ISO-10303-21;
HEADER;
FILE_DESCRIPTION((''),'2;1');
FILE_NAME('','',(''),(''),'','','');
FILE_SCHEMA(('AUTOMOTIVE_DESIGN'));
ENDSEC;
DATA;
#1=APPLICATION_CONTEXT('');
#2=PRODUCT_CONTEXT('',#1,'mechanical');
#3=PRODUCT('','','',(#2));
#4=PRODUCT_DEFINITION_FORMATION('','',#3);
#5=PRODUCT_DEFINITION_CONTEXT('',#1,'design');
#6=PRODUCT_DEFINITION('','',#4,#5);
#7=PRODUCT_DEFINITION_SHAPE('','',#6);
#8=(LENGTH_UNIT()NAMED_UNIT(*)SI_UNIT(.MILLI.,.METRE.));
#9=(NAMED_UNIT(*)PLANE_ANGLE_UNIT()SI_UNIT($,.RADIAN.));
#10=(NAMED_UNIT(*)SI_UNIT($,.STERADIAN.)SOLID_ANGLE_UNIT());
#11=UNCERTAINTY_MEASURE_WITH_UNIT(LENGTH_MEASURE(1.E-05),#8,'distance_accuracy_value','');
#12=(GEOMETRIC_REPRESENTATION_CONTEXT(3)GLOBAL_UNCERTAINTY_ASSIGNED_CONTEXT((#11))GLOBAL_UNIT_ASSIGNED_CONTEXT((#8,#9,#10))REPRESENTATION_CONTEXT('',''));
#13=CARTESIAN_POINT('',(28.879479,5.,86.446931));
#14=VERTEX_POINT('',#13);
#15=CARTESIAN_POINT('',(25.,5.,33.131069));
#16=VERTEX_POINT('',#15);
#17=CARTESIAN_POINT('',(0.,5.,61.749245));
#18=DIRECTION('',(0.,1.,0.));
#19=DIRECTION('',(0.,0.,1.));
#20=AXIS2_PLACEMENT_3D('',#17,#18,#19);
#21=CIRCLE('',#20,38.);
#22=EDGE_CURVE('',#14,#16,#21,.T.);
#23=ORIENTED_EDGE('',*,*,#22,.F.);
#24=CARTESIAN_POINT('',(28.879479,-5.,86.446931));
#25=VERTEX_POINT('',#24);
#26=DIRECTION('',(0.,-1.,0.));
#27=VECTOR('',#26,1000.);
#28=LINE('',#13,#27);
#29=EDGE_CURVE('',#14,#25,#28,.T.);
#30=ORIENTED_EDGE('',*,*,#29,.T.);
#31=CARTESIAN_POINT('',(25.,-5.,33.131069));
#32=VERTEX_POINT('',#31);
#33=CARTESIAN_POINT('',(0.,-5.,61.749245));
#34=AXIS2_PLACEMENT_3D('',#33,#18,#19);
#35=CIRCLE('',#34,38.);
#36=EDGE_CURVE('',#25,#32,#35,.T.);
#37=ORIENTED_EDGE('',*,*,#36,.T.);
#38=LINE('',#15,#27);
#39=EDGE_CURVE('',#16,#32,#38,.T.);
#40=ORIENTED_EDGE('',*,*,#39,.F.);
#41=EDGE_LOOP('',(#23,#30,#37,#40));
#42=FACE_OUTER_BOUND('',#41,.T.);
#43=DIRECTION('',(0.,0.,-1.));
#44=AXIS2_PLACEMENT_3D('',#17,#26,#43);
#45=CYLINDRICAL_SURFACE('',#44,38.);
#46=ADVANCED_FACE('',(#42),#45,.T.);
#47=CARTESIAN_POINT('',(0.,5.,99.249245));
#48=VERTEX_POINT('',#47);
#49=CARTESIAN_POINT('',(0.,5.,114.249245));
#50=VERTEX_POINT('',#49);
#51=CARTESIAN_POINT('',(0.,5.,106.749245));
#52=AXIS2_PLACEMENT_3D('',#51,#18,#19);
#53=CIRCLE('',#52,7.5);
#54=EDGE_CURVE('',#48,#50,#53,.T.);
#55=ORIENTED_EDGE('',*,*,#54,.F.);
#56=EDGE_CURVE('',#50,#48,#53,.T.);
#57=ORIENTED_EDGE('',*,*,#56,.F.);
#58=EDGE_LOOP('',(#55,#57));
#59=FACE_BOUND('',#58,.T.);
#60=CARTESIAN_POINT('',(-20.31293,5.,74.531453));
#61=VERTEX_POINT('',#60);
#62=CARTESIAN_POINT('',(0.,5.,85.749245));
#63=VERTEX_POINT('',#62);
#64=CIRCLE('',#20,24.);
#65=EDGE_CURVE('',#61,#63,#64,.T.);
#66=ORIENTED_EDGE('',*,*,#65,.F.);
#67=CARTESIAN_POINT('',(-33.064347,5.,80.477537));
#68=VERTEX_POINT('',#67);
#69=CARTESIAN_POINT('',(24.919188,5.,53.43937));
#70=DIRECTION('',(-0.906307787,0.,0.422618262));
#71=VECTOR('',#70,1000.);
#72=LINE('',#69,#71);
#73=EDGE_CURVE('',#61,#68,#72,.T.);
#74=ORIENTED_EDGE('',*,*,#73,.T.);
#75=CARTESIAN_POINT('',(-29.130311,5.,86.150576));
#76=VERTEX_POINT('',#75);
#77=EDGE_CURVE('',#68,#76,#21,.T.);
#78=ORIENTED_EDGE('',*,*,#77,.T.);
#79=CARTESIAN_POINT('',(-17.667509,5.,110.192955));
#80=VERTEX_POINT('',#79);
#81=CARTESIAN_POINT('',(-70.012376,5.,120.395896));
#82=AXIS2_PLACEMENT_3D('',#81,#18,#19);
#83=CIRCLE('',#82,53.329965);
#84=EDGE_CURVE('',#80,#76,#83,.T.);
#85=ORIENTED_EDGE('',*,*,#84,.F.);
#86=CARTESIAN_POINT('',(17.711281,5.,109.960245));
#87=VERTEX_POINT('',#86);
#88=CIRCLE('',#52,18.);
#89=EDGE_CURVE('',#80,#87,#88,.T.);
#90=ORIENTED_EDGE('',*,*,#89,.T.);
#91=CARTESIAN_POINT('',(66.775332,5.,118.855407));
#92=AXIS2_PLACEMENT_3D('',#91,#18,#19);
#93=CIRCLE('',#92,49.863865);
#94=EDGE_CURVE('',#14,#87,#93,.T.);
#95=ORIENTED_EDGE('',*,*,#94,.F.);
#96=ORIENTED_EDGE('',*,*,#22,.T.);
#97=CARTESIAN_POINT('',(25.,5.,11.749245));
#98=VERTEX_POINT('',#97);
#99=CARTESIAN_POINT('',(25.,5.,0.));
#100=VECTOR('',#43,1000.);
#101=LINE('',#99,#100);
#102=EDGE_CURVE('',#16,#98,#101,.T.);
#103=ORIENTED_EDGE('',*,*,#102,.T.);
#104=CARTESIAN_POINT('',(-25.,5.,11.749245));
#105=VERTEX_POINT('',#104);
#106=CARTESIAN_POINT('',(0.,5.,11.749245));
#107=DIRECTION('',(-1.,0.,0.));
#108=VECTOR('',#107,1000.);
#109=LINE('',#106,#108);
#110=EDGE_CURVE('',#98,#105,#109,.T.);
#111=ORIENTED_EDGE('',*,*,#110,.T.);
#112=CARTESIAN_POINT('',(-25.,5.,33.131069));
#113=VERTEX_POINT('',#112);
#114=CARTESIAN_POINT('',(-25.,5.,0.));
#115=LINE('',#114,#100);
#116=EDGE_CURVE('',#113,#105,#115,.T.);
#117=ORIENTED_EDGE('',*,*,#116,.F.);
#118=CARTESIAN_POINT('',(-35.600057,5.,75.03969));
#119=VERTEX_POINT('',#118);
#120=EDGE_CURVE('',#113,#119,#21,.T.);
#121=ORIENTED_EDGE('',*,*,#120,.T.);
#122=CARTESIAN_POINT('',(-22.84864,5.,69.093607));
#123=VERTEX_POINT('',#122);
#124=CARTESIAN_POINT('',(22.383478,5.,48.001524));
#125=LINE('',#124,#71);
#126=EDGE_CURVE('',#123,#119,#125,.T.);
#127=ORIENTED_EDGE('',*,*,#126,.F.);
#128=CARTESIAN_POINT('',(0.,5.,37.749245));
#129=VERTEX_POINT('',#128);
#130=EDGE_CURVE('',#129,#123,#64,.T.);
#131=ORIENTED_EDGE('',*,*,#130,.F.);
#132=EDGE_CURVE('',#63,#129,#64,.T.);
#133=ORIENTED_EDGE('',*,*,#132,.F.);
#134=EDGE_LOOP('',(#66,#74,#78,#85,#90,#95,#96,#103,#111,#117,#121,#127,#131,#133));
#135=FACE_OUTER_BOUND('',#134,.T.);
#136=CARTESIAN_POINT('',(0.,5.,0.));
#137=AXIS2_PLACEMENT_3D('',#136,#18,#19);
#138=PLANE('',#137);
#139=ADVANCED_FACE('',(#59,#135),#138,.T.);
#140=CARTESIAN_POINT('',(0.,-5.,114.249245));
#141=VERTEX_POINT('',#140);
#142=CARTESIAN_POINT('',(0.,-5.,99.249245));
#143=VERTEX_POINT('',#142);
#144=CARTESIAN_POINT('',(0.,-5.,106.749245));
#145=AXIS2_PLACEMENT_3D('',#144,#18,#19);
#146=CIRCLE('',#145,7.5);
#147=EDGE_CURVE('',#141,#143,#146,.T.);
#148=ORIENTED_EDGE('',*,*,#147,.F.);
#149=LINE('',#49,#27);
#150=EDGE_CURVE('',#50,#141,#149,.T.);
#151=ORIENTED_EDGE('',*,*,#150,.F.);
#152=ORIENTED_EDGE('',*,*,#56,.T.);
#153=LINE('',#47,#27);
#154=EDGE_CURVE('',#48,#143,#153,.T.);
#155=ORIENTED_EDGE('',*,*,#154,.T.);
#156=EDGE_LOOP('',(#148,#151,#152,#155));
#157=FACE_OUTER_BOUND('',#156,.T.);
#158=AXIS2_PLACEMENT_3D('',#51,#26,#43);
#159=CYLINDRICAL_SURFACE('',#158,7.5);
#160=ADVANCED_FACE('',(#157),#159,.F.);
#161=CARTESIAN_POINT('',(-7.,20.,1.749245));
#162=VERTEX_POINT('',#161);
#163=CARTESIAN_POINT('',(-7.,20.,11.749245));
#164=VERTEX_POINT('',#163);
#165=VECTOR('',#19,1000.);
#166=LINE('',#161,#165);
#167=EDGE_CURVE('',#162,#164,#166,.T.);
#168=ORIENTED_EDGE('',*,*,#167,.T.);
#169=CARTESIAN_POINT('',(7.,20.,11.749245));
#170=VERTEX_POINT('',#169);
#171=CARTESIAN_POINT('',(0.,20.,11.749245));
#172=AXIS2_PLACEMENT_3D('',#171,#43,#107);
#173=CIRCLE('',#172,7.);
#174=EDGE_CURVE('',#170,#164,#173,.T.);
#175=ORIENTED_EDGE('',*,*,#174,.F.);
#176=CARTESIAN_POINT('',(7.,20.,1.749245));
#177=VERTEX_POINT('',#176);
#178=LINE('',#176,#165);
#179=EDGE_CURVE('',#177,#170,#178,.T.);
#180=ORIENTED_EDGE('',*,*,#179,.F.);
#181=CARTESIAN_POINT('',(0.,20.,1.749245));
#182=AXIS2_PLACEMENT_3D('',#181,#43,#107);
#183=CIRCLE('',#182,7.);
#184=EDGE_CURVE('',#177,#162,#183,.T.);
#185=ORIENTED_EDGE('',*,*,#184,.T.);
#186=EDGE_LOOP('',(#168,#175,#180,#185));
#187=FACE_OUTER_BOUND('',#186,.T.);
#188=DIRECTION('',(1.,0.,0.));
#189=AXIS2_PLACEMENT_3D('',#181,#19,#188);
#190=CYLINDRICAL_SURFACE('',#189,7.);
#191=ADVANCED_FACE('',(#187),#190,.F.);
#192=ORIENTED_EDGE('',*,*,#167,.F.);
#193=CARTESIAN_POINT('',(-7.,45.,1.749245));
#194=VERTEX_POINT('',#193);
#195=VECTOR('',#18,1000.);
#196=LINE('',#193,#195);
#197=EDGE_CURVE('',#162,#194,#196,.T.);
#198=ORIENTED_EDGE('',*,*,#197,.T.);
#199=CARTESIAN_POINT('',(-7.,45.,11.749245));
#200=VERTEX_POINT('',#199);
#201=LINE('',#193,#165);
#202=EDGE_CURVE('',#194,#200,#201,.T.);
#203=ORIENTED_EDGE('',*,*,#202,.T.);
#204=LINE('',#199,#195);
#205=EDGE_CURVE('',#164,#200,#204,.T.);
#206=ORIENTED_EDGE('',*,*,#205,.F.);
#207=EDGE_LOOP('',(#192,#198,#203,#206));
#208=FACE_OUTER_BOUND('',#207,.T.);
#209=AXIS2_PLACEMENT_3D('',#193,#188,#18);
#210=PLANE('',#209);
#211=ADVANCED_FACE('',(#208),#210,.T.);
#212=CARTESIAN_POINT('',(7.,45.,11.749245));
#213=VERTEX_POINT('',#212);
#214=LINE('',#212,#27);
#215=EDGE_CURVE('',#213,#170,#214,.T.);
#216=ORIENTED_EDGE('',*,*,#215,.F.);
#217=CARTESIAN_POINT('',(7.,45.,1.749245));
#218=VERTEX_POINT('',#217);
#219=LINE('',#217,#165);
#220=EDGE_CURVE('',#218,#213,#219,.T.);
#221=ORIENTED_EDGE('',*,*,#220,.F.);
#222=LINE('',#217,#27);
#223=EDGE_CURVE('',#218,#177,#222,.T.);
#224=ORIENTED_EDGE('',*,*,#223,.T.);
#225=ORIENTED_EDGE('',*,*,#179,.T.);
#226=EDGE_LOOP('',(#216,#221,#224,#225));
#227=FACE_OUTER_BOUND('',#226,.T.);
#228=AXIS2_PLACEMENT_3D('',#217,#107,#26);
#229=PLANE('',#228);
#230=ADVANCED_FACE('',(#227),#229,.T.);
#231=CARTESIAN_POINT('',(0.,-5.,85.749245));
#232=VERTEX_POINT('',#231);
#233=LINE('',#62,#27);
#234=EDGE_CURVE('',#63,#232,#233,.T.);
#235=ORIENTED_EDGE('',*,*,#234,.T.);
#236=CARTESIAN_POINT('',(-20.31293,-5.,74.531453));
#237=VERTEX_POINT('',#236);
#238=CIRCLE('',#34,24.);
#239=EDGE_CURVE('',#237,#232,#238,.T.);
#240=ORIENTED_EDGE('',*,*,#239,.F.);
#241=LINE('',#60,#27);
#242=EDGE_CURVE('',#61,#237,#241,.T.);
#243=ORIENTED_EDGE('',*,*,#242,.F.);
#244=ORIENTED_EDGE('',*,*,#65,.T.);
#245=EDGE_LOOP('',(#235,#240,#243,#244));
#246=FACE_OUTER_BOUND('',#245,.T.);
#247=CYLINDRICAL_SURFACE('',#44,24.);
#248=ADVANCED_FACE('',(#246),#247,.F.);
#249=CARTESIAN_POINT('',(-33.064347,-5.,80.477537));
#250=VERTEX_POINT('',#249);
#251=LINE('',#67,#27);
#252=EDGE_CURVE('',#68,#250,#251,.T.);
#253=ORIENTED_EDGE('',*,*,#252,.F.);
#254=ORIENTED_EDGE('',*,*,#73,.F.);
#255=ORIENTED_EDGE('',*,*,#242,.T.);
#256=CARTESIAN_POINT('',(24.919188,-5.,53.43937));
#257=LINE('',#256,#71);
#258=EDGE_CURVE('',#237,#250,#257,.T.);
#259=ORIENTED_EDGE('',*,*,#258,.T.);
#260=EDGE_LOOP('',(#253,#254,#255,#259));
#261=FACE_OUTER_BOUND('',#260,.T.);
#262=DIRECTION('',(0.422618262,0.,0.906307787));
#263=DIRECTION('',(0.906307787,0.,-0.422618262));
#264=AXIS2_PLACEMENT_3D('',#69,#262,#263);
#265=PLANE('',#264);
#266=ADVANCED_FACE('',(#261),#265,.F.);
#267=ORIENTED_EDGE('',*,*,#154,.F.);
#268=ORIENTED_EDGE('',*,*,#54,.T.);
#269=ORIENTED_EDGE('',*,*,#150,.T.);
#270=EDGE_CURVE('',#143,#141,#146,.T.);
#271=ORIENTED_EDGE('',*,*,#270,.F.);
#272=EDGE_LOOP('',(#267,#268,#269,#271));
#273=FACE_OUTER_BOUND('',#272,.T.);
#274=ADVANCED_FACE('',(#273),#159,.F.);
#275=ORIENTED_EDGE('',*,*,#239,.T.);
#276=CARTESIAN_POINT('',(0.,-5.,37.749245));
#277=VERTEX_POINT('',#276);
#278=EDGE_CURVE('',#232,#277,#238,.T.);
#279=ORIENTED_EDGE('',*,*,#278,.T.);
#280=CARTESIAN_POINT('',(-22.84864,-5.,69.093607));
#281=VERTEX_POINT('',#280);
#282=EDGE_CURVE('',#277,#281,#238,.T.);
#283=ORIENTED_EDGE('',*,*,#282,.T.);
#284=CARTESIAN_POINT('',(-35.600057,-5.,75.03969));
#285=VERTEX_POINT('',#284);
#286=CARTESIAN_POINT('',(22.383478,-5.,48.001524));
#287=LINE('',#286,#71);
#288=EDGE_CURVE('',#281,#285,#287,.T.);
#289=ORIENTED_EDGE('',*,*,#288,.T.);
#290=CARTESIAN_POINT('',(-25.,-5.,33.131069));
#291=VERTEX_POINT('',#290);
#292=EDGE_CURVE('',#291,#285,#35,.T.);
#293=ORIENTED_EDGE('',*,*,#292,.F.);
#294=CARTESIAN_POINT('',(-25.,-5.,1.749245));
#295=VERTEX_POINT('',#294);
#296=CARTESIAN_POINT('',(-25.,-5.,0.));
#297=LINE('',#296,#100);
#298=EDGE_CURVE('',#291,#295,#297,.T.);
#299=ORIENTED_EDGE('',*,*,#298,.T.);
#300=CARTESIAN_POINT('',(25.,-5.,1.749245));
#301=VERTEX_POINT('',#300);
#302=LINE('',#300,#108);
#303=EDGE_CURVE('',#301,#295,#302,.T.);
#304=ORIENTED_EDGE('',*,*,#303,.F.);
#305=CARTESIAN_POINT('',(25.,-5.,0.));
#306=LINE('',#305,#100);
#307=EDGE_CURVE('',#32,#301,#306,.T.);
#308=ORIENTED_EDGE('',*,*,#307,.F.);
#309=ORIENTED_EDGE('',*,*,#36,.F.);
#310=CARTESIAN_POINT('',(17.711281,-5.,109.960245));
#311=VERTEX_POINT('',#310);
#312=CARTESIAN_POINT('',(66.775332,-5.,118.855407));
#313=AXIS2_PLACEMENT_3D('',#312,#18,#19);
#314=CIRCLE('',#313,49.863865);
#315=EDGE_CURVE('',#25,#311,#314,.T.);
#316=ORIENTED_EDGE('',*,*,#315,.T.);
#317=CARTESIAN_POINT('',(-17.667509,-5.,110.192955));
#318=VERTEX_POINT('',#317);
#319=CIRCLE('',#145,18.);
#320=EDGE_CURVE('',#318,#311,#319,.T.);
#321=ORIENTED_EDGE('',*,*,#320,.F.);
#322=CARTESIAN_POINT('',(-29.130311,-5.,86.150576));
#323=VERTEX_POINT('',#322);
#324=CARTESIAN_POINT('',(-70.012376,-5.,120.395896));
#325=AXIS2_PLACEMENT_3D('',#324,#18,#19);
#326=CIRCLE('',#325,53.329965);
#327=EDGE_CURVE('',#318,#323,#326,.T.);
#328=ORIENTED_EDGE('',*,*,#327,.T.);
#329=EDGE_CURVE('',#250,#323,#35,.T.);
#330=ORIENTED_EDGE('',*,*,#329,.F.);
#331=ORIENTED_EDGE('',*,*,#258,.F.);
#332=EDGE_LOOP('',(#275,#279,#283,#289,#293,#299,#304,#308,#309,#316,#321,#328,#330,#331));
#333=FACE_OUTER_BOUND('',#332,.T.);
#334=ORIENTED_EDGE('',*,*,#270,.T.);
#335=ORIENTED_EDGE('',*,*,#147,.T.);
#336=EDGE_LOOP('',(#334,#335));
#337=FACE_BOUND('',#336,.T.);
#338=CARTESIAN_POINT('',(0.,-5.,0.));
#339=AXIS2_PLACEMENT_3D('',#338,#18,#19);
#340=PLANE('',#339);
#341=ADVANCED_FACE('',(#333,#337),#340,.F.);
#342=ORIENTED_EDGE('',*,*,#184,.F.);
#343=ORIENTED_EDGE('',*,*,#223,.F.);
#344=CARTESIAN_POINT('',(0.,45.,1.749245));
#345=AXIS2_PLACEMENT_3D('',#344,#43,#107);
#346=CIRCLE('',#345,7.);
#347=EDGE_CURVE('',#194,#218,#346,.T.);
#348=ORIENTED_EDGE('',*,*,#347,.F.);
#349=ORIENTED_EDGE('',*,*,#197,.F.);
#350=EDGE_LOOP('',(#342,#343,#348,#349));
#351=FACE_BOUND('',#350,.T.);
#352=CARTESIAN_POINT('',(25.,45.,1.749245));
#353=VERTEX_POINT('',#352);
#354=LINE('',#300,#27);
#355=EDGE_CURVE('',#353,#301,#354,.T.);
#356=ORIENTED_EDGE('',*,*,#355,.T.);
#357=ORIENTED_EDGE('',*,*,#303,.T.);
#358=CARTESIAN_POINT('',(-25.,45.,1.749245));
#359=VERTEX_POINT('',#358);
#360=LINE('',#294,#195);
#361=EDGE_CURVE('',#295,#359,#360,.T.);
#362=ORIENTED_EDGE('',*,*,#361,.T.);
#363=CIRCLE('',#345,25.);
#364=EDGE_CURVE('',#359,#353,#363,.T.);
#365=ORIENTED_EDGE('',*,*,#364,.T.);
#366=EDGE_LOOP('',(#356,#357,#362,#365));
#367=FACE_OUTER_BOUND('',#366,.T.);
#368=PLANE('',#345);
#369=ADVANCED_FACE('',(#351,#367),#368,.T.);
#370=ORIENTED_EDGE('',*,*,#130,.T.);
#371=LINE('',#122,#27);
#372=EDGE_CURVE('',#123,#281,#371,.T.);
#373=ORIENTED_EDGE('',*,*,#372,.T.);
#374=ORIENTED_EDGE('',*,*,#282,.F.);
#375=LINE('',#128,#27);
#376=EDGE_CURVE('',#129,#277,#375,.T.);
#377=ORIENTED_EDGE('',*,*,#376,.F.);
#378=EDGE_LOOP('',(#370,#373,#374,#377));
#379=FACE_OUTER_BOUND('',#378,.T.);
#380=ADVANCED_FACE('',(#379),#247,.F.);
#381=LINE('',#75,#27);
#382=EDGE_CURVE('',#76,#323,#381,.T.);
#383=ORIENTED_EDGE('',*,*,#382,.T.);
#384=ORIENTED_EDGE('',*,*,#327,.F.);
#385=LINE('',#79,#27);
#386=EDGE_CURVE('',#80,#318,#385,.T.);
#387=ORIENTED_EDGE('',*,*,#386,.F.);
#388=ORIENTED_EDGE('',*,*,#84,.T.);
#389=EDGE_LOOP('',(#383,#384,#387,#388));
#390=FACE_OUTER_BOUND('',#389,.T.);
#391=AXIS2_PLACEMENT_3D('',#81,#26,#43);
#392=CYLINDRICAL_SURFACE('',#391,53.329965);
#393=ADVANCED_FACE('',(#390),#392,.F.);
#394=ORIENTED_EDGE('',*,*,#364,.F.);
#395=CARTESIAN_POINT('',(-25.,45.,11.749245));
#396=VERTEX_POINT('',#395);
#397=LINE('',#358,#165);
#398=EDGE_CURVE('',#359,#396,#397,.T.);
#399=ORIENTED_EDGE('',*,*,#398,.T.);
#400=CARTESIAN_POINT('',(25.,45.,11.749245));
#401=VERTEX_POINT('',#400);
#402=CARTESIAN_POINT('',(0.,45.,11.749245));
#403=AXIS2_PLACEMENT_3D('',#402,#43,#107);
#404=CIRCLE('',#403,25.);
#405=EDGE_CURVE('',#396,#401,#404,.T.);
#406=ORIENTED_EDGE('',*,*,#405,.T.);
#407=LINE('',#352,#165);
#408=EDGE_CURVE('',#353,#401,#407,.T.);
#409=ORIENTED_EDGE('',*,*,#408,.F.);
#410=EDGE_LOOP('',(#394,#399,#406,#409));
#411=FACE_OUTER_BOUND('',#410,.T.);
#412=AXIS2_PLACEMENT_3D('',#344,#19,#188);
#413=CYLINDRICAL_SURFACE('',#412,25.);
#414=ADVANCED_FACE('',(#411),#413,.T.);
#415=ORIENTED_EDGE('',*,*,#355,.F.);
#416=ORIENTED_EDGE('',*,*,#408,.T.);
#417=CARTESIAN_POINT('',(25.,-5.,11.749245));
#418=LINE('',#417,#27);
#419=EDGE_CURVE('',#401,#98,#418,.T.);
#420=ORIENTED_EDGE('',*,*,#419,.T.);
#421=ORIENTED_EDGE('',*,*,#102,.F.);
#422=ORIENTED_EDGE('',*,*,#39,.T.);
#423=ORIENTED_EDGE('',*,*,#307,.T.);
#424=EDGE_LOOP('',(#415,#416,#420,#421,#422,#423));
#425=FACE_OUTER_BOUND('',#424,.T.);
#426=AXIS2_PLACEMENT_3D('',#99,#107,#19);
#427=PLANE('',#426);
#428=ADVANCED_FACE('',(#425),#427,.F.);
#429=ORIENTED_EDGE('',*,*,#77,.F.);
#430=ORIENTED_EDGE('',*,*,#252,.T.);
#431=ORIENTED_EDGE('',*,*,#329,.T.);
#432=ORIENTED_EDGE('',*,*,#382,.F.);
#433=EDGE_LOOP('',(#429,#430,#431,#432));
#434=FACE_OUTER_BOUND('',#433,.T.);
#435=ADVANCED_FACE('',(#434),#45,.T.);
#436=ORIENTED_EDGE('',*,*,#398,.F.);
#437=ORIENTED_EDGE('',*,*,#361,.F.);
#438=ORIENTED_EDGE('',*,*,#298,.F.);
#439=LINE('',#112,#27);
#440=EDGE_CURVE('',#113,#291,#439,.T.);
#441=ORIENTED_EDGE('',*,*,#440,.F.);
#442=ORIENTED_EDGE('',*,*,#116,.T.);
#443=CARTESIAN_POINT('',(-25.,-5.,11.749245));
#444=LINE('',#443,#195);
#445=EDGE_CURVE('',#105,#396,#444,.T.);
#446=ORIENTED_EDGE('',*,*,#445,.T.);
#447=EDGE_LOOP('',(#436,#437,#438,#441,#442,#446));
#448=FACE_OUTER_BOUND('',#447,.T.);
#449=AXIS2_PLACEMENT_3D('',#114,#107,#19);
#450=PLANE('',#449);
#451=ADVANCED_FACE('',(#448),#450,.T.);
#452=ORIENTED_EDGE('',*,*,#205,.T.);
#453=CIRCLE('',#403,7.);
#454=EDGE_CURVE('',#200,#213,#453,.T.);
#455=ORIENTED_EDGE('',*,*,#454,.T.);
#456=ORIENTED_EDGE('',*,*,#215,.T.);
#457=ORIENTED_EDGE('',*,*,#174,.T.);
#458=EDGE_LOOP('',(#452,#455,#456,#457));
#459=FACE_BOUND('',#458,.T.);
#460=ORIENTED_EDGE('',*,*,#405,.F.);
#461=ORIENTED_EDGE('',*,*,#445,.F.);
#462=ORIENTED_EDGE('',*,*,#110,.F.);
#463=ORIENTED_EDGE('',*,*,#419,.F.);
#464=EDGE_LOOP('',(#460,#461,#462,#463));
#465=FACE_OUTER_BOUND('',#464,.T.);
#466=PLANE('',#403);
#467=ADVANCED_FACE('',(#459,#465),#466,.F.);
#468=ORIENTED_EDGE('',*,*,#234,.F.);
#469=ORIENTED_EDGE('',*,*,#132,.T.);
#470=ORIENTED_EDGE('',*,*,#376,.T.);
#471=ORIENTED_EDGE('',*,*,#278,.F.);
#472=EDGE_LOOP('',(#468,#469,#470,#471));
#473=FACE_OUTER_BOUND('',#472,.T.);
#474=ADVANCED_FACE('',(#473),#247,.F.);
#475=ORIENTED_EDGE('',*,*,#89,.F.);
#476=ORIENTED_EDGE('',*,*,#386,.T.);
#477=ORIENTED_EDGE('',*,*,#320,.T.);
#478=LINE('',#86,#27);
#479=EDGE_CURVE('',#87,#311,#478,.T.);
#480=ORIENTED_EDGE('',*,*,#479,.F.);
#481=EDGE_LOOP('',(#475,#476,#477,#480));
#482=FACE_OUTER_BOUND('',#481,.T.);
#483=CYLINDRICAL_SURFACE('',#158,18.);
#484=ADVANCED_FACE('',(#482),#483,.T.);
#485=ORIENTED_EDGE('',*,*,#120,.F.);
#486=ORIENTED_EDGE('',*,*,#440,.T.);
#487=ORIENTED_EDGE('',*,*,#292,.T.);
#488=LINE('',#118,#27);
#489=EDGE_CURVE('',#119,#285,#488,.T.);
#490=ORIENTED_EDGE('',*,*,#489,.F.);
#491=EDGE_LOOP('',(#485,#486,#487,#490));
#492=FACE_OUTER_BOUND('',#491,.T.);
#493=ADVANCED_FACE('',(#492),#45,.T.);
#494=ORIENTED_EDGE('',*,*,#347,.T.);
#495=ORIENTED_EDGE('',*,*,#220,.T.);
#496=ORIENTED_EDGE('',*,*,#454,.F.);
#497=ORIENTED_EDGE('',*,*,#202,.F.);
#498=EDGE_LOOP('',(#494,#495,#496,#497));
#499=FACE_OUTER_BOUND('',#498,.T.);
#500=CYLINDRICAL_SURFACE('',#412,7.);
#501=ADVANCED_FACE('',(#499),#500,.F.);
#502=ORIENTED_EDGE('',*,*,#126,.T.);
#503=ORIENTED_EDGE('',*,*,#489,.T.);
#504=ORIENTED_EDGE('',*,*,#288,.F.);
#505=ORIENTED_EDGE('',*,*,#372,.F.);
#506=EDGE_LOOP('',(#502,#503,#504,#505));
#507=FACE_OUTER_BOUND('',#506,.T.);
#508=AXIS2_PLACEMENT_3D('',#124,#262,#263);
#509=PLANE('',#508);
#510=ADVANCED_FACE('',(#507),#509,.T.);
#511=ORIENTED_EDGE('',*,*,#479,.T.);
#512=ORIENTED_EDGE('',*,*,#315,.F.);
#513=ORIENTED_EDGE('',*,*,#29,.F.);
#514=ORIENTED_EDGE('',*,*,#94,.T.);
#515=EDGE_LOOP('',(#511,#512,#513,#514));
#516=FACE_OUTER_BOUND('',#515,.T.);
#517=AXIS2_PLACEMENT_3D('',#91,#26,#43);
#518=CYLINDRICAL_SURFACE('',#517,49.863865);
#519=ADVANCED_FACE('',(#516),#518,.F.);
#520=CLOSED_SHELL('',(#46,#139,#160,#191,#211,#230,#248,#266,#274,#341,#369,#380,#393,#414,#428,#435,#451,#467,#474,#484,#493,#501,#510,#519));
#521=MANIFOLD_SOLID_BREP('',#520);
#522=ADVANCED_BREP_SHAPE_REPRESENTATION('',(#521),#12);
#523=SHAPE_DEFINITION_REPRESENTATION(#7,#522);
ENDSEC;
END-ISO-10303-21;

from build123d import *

# Parameters (mm, degrees)
CLAMP_BASE_PROFILE_SKETCH_R = 7.5
CLAMP_BASE_PLATE_DEPTH      = 5
SLOTTED_UPRIGHT_TAB_DEPTH   = 10


with BuildPart() as part:
    # Clamp Base Profile Sketch → Clamp Base Plate (new, symmetric)
    with BuildSketch(Plane(origin=(0, 0, 0), x_dir=(1, 0, 0), z_dir=(0, 1, 0))):
        with BuildLine():
            Line((-25, -33.131068574), (-25, -11.749244617))
            Line((-25, -11.749244617), (25, -11.749244617))
            Line((25, -11.749244617), (25, -33.131068574))
            ThreePointArc((25, -33.131068574), (37.899800142, -58.991501114), (28.879478838, -86.446930784))
            ThreePointArc((28.879478838, -86.446930784), (21.733959657, -97.461955057), (17.711280988, -109.960245356))
            ThreePointArc((17.711280988, -109.960245356), (0.118395162, -124.74885524), (-17.667508621, -110.192954697))
            ThreePointArc((-17.667508621, -110.192954697), (-21.873782153, -97.444622756), (-29.130311117, -86.150576019))
            ThreePointArc((-29.130311117, -86.150576019), (-31.226426819, -83.403580628), (-33.064347445, -80.477536799))
            Line((-33.064347445, -80.477536799), (-20.312930357, -74.531453358))
            ThreePointArc((-20.312930357, -74.531453358), (21.751386889, -51.606406335), (-22.848639927, -69.093606636))
            Line((-22.848639927, -69.093606636), (-35.600057015, -75.039690077))
            ThreePointArc((-35.600057015, -75.039690077), (-36.839854324, -52.431244113), (-25, -33.131068574))
        make_face()
        with Locations(Location((0, -106.749244617, 0), (0, 0, 270))):
            Circle(CLAMP_BASE_PROFILE_SKETCH_R, mode=Mode.SUBTRACT)
    extrude(amount=CLAMP_BASE_PLATE_DEPTH, both=True)

    # Slotted Tab Profile Sketch → Slotted Upright Tab (add)
    with BuildSketch(Plane(origin=(0, 0, 11.749244617), x_dir=(-1, 0, 0), z_dir=(0, 0, -1))):
        with BuildLine():
            Line((-25, -5), (-25, 45))
            ThreePointArc((-25, 45), (0, 70), (25, 45))
            Line((25, 45), (25, -5))
            Line((25, -5), (-25, -5))
        make_face()
        with BuildLine():
            Line((7, 45), (7, 20))
            ThreePointArc((7, 20), (0, 13), (-7, 20))
            Line((-7, 20), (-7, 45))
            ThreePointArc((-7, 45), (0, 52), (7, 45))
        make_face(mode=Mode.SUBTRACT)
    extrude(amount=SLOTTED_UPRIGHT_TAB_DEPTH)


solid = part.part
